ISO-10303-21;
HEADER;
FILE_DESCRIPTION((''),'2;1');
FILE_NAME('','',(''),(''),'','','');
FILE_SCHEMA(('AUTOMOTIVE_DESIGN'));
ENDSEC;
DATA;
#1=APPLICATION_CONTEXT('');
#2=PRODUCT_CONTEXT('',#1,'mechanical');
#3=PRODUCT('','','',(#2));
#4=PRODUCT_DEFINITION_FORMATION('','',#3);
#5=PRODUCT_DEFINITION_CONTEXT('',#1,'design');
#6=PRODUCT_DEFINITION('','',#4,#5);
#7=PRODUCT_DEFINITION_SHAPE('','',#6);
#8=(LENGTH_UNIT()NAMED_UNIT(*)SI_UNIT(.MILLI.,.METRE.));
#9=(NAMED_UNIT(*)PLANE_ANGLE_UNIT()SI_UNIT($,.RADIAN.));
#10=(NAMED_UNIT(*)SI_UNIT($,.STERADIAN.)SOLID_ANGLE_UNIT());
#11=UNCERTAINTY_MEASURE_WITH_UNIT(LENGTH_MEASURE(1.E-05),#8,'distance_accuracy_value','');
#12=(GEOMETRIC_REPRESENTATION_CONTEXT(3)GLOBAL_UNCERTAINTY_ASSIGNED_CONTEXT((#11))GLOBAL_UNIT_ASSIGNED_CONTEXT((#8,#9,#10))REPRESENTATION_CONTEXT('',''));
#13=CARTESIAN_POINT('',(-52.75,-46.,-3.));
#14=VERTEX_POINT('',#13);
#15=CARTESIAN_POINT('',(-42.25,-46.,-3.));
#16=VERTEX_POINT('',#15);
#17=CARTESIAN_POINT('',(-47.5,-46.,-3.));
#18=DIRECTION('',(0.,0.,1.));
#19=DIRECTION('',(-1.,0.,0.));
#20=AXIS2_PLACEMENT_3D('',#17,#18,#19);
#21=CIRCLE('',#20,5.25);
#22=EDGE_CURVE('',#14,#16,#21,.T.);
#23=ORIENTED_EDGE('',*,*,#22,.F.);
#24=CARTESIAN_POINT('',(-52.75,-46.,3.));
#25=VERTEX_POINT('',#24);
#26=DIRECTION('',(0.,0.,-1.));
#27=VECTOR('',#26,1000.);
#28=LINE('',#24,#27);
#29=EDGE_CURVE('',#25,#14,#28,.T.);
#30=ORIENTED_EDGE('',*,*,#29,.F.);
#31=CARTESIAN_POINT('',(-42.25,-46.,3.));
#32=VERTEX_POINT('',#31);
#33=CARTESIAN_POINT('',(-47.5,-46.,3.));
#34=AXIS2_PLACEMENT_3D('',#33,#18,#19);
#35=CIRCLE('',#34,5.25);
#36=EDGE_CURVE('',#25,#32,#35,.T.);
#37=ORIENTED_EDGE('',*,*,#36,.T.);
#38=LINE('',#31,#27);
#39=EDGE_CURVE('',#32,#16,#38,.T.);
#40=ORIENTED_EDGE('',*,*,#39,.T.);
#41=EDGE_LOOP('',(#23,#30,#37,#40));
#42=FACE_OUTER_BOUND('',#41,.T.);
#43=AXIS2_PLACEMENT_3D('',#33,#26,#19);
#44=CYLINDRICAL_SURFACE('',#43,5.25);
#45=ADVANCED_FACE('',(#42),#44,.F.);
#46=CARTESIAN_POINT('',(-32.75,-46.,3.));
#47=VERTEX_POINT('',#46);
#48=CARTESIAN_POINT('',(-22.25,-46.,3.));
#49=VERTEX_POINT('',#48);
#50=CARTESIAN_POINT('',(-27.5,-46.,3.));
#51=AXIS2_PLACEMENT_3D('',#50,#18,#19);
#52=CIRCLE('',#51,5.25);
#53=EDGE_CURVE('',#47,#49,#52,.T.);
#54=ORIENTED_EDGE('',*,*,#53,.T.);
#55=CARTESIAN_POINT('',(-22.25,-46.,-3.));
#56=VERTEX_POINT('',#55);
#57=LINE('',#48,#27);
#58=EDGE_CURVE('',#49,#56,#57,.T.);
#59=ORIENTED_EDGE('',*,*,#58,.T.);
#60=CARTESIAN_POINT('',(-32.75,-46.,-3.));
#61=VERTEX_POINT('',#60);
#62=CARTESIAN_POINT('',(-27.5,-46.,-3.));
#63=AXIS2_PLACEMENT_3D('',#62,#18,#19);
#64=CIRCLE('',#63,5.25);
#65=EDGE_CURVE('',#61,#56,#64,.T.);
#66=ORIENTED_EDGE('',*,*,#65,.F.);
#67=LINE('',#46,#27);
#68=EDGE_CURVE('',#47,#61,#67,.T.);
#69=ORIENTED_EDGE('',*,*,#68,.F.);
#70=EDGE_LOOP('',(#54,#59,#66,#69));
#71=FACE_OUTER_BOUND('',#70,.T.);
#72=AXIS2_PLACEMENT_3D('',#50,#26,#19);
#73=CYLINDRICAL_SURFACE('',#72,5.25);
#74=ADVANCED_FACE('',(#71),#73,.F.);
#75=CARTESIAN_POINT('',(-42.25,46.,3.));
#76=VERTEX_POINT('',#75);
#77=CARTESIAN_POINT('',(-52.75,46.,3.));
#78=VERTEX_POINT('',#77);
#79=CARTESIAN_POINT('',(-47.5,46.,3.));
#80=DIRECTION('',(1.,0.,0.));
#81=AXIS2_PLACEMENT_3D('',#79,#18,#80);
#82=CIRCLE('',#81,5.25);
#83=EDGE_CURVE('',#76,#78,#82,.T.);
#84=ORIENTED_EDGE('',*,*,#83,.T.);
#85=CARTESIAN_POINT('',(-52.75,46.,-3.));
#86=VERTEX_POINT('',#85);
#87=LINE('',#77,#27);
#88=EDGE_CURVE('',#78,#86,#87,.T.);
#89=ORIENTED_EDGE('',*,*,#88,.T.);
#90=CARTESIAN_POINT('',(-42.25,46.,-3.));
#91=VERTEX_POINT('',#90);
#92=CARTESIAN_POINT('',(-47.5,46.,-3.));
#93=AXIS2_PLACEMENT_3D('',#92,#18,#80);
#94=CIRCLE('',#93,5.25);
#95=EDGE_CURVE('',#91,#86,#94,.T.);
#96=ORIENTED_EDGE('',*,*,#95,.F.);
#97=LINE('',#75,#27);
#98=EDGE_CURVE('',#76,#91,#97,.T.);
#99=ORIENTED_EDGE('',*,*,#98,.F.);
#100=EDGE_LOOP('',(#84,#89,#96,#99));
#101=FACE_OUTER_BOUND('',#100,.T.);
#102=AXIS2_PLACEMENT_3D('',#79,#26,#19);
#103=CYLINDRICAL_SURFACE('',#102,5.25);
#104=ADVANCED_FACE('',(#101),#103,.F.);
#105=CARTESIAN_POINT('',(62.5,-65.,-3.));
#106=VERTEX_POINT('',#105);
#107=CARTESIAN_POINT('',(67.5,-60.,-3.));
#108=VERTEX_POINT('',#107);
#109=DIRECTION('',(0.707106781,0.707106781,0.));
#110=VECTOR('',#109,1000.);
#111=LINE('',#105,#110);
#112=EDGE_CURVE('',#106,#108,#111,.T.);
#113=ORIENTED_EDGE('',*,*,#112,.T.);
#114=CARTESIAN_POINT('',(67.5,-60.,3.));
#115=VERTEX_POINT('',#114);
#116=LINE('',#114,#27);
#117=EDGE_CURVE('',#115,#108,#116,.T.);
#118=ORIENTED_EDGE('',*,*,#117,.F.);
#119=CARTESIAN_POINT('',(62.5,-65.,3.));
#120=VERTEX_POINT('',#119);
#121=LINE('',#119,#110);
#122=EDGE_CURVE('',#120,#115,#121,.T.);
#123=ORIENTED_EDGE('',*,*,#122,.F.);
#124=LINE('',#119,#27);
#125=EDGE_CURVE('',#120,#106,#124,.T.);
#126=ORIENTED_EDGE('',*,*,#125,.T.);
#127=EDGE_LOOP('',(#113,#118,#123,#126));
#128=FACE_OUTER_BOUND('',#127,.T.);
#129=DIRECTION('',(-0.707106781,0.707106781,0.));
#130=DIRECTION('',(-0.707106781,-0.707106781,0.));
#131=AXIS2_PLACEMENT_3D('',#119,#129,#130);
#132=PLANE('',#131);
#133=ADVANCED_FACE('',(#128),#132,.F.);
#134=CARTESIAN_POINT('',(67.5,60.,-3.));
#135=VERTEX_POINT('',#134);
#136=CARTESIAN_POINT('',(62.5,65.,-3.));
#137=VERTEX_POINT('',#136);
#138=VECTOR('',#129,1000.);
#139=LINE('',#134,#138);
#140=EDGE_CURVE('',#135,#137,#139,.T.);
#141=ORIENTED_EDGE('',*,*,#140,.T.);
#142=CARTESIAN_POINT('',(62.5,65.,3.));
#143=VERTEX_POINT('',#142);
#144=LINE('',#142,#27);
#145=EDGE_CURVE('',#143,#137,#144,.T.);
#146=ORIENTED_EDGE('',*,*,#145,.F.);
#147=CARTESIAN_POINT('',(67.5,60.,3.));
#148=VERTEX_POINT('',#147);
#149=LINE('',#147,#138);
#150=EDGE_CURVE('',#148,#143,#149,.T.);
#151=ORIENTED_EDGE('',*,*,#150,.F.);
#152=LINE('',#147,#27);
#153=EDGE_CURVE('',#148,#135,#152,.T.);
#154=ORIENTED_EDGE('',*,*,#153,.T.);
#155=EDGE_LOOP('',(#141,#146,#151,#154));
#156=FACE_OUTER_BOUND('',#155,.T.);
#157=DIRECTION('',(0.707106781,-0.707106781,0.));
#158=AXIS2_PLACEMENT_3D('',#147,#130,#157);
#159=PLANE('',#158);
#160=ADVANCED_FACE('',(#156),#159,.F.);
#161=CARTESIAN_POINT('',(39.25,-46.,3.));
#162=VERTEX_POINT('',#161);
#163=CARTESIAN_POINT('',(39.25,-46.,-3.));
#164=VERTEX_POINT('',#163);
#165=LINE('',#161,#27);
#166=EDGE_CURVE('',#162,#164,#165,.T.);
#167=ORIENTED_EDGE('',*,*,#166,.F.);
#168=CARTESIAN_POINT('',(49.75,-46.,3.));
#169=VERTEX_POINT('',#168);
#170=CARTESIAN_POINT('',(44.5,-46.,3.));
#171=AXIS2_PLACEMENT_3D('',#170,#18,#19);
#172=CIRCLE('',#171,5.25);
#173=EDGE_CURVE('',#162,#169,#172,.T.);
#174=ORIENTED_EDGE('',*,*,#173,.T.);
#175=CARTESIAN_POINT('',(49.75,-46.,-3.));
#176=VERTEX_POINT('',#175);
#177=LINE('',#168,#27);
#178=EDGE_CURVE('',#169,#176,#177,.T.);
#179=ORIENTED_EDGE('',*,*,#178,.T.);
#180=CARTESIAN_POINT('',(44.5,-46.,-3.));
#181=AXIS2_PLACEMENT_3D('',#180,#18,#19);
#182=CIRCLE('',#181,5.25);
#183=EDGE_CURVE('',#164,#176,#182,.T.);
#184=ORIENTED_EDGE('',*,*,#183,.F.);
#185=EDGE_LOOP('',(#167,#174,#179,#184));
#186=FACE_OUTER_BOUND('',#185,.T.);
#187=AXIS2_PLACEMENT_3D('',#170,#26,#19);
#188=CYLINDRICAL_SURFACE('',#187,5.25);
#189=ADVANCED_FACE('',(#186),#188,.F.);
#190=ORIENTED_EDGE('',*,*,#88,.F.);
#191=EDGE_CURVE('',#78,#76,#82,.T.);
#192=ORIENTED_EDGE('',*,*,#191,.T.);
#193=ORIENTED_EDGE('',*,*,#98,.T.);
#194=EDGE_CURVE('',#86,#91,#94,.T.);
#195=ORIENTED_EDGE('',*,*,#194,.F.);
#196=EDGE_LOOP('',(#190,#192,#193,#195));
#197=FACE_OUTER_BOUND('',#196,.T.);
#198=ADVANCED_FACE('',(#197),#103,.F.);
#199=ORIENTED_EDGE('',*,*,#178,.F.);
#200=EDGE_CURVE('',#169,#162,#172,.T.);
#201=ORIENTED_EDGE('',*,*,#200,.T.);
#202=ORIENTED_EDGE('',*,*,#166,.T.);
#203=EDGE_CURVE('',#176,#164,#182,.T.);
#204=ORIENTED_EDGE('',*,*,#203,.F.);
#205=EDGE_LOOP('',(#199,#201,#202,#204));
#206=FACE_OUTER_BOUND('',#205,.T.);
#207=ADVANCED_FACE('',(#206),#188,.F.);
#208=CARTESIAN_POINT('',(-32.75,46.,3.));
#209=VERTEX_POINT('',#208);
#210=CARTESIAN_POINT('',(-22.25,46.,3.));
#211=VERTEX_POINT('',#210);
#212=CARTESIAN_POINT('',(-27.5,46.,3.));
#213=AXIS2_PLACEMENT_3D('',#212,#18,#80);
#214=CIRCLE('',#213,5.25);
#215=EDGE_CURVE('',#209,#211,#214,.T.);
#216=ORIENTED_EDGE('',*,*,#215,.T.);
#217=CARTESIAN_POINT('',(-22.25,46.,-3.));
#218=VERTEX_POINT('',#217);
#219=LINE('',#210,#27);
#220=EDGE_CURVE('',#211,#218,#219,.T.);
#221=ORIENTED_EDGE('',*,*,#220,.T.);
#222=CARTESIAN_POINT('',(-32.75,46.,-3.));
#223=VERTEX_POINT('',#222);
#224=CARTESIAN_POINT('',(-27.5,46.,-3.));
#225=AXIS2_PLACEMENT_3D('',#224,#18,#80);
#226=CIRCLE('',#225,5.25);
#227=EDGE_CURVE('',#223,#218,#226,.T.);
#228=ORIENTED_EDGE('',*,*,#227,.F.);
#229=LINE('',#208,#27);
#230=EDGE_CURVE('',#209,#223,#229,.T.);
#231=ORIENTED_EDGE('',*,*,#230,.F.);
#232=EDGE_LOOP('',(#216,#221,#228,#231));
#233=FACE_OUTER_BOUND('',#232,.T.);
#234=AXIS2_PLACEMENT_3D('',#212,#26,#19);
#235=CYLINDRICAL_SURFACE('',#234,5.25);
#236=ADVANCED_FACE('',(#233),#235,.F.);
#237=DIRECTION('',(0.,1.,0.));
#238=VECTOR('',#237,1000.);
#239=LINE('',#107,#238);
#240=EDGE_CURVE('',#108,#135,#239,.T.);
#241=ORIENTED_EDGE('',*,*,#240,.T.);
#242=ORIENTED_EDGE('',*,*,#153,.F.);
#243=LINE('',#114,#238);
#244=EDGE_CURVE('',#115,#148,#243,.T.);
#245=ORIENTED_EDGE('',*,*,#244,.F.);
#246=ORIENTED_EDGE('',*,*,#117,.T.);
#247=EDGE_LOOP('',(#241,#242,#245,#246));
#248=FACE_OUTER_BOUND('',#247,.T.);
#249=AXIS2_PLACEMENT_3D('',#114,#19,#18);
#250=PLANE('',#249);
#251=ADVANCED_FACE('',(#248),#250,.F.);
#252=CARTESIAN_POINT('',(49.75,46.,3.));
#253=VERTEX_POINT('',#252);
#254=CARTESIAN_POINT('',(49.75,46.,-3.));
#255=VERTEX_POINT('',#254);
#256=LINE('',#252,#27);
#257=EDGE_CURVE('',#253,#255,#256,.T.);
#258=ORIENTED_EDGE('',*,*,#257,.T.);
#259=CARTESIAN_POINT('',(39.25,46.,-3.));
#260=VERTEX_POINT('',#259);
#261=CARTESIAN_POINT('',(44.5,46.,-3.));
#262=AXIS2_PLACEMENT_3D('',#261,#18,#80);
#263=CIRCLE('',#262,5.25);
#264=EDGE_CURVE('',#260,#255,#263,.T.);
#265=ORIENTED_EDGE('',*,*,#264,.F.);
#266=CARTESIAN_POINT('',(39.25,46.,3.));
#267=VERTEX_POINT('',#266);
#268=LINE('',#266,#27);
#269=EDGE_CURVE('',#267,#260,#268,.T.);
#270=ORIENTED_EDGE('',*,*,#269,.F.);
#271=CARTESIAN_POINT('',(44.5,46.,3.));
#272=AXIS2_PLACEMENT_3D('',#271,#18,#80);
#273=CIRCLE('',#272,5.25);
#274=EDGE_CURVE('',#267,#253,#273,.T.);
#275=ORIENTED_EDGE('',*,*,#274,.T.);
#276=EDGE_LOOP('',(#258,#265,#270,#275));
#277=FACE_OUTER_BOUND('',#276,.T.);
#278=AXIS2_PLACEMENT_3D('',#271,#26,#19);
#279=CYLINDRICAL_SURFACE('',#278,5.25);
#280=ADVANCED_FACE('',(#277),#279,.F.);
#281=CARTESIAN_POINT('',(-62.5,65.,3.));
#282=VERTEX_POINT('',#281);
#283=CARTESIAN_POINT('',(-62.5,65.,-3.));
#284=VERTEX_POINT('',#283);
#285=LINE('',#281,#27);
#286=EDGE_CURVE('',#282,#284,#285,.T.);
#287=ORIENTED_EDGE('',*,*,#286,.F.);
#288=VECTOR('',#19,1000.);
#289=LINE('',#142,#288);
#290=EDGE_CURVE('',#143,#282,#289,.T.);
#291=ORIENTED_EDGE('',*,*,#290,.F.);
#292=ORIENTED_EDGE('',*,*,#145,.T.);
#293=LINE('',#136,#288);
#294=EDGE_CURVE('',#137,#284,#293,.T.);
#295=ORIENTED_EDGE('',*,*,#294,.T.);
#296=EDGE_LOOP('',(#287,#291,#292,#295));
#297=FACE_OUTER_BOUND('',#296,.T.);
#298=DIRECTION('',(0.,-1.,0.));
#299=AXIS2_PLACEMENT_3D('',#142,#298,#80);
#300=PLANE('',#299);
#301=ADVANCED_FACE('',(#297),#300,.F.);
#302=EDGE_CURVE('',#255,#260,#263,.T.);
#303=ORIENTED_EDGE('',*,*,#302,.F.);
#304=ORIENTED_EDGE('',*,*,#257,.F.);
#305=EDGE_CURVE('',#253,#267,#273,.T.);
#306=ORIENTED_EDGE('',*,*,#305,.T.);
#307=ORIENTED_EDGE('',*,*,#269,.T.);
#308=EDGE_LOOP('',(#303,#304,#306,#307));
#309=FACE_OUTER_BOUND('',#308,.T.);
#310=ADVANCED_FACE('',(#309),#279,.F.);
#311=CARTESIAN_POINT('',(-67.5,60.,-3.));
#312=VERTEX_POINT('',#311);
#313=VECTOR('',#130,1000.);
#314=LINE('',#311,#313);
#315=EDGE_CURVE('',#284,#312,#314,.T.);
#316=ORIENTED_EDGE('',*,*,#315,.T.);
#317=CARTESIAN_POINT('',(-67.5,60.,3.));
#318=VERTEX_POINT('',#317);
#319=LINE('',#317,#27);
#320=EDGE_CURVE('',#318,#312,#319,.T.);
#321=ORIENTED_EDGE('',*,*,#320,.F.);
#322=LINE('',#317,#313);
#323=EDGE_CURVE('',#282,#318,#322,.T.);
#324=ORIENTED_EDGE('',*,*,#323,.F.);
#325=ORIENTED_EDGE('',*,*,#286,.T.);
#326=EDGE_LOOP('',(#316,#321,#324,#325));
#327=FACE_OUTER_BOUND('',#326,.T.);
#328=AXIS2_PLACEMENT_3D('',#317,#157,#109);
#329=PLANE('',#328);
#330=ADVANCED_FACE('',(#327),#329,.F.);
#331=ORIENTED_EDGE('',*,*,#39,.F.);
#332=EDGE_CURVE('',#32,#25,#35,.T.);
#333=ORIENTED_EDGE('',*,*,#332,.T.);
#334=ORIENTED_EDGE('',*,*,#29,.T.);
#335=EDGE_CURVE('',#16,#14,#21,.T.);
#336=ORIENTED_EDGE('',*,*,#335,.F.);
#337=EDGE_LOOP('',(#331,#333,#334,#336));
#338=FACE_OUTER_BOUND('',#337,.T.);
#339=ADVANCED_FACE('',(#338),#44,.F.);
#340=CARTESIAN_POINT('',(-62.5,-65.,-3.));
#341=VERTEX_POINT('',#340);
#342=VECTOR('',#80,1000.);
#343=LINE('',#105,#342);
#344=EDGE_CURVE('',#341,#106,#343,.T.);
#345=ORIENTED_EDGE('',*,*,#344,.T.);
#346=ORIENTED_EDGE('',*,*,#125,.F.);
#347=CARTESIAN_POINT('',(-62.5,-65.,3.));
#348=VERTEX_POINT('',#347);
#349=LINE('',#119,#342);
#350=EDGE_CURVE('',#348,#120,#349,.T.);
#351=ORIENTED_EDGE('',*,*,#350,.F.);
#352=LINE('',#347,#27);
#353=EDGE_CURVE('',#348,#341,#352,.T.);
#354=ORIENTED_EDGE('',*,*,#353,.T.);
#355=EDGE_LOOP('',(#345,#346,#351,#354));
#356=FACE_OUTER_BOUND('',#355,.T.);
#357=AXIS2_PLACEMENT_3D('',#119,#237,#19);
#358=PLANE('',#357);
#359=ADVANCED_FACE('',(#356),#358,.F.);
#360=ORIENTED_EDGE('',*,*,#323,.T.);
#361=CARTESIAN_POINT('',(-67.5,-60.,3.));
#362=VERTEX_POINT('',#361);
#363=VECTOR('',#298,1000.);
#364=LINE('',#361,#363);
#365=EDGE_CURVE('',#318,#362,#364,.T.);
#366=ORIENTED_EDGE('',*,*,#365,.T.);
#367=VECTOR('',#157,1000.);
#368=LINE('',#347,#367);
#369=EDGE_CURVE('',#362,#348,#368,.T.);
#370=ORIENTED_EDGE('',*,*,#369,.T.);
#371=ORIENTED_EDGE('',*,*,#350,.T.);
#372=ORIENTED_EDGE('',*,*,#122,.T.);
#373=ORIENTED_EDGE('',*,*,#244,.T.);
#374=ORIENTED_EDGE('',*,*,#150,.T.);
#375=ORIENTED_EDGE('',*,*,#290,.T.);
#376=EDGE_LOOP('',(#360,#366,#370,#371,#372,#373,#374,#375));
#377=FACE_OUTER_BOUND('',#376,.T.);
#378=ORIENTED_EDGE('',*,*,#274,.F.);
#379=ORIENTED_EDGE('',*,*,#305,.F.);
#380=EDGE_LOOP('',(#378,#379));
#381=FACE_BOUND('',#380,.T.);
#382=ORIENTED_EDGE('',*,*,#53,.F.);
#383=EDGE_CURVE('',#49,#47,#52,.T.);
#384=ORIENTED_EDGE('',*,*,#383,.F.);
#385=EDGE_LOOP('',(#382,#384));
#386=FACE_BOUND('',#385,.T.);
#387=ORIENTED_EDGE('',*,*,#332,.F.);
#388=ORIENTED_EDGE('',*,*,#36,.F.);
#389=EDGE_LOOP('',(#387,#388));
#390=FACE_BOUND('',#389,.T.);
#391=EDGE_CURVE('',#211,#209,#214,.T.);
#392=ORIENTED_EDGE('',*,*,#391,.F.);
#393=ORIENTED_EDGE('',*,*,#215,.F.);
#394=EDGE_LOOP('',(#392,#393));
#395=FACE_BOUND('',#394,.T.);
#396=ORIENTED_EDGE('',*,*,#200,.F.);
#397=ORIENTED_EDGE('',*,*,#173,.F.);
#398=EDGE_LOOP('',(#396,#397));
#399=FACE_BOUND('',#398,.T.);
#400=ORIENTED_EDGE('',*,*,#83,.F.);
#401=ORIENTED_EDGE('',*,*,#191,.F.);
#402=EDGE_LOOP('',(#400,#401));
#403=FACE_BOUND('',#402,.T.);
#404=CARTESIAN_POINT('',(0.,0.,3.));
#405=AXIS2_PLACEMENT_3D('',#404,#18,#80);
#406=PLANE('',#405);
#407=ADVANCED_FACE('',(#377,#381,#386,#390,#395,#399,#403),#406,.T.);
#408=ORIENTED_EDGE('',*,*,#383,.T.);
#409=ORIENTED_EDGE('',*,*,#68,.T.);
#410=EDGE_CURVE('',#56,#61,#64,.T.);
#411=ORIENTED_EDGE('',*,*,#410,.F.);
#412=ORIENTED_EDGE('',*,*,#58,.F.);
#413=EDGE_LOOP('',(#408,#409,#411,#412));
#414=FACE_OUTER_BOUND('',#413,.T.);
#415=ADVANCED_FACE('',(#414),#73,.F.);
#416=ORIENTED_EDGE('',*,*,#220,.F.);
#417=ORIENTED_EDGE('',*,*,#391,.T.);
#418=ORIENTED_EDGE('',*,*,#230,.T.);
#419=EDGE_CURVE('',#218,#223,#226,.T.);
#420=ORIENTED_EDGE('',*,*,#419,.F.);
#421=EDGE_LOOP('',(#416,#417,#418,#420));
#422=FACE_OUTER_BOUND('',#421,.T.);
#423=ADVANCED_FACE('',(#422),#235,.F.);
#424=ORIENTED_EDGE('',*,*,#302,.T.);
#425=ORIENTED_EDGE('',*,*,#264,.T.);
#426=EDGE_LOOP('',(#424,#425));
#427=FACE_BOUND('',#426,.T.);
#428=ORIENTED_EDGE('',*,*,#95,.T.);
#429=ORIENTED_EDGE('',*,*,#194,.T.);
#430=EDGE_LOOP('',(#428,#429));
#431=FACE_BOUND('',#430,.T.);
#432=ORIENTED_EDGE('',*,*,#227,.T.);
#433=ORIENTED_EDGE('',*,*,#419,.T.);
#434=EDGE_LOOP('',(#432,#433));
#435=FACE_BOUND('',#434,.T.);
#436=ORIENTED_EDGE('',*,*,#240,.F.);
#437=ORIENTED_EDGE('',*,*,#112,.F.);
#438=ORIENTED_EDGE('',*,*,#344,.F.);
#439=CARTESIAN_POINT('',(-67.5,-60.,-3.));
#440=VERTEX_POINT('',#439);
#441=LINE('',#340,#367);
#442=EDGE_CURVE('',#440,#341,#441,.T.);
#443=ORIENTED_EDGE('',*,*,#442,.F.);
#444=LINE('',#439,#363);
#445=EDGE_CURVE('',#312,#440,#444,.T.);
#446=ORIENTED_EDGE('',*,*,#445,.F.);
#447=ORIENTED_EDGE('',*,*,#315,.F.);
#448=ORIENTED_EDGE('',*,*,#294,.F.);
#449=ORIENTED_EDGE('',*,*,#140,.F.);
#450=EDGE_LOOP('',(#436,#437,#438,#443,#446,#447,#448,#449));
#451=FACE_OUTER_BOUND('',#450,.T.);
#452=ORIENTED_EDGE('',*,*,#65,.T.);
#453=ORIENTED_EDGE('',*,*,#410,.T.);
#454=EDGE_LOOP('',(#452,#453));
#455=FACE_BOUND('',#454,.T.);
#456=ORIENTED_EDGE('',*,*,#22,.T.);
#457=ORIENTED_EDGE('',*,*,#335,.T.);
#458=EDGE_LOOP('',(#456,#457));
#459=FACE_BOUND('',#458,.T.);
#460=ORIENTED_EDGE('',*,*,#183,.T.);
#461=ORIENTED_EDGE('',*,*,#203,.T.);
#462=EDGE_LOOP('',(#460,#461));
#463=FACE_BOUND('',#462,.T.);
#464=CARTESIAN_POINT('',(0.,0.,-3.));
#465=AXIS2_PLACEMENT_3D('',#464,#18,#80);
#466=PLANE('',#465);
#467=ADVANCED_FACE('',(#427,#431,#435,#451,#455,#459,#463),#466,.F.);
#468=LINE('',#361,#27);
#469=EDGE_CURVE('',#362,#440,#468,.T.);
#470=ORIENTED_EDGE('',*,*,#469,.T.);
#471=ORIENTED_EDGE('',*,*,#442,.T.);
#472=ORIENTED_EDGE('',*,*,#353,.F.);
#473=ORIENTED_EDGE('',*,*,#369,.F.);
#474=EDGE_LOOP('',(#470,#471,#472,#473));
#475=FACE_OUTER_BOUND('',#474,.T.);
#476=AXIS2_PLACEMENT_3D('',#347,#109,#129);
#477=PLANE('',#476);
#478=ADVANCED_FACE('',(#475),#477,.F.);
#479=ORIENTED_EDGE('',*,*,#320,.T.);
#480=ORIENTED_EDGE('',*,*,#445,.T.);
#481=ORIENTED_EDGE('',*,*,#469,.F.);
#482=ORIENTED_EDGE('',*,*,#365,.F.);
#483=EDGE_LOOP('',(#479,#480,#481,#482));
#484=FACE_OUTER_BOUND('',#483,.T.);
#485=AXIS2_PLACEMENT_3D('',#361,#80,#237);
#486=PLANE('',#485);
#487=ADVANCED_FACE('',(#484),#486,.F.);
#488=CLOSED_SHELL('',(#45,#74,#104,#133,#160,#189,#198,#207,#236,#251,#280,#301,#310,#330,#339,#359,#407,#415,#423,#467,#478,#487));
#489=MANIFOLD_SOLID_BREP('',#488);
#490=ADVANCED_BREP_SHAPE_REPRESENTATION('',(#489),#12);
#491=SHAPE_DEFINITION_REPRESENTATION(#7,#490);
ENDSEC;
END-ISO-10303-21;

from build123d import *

# Parameters (mm, degrees)
SKETCH1_R           = 5.25
BOSS_EXTRUDE1_DEPTH = 3


with BuildPart() as part:
    # Sketch1 → Boss-Extrude1 (new, symmetric)
    with BuildSketch(Plane.XY):
        Polygon((-67.5, 60), (-62.5, 65), (62.5, 65), (67.5, 60), (67.5, -60), (62.5, -65), (-62.5, -65), (-67.5, -60), align=None)
        with Locations((-47.5, 46)):
            Circle(SKETCH1_R, mode=Mode.SUBTRACT)
        with Locations((-27.5, 46)):
            Circle(SKETCH1_R, mode=Mode.SUBTRACT)
        with Locations((44.5, 46)):
            Circle(SKETCH1_R, mode=Mode.SUBTRACT)
        with Locations(Location((44.5, -46, 0), (0, 0, 180))):
            Circle(SKETCH1_R, mode=Mode.SUBTRACT)
        with Locations(Location((-27.5, -46, 0), (0, 0, 180))):
            Circle(SKETCH1_R, mode=Mode.SUBTRACT)
        with Locations(Location((-47.5, -46, 0), (0, 0, 180))):
            Circle(SKETCH1_R, mode=Mode.SUBTRACT)
    extrude(amount=BOSS_EXTRUDE1_DEPTH, both=True)


solid = part.part
